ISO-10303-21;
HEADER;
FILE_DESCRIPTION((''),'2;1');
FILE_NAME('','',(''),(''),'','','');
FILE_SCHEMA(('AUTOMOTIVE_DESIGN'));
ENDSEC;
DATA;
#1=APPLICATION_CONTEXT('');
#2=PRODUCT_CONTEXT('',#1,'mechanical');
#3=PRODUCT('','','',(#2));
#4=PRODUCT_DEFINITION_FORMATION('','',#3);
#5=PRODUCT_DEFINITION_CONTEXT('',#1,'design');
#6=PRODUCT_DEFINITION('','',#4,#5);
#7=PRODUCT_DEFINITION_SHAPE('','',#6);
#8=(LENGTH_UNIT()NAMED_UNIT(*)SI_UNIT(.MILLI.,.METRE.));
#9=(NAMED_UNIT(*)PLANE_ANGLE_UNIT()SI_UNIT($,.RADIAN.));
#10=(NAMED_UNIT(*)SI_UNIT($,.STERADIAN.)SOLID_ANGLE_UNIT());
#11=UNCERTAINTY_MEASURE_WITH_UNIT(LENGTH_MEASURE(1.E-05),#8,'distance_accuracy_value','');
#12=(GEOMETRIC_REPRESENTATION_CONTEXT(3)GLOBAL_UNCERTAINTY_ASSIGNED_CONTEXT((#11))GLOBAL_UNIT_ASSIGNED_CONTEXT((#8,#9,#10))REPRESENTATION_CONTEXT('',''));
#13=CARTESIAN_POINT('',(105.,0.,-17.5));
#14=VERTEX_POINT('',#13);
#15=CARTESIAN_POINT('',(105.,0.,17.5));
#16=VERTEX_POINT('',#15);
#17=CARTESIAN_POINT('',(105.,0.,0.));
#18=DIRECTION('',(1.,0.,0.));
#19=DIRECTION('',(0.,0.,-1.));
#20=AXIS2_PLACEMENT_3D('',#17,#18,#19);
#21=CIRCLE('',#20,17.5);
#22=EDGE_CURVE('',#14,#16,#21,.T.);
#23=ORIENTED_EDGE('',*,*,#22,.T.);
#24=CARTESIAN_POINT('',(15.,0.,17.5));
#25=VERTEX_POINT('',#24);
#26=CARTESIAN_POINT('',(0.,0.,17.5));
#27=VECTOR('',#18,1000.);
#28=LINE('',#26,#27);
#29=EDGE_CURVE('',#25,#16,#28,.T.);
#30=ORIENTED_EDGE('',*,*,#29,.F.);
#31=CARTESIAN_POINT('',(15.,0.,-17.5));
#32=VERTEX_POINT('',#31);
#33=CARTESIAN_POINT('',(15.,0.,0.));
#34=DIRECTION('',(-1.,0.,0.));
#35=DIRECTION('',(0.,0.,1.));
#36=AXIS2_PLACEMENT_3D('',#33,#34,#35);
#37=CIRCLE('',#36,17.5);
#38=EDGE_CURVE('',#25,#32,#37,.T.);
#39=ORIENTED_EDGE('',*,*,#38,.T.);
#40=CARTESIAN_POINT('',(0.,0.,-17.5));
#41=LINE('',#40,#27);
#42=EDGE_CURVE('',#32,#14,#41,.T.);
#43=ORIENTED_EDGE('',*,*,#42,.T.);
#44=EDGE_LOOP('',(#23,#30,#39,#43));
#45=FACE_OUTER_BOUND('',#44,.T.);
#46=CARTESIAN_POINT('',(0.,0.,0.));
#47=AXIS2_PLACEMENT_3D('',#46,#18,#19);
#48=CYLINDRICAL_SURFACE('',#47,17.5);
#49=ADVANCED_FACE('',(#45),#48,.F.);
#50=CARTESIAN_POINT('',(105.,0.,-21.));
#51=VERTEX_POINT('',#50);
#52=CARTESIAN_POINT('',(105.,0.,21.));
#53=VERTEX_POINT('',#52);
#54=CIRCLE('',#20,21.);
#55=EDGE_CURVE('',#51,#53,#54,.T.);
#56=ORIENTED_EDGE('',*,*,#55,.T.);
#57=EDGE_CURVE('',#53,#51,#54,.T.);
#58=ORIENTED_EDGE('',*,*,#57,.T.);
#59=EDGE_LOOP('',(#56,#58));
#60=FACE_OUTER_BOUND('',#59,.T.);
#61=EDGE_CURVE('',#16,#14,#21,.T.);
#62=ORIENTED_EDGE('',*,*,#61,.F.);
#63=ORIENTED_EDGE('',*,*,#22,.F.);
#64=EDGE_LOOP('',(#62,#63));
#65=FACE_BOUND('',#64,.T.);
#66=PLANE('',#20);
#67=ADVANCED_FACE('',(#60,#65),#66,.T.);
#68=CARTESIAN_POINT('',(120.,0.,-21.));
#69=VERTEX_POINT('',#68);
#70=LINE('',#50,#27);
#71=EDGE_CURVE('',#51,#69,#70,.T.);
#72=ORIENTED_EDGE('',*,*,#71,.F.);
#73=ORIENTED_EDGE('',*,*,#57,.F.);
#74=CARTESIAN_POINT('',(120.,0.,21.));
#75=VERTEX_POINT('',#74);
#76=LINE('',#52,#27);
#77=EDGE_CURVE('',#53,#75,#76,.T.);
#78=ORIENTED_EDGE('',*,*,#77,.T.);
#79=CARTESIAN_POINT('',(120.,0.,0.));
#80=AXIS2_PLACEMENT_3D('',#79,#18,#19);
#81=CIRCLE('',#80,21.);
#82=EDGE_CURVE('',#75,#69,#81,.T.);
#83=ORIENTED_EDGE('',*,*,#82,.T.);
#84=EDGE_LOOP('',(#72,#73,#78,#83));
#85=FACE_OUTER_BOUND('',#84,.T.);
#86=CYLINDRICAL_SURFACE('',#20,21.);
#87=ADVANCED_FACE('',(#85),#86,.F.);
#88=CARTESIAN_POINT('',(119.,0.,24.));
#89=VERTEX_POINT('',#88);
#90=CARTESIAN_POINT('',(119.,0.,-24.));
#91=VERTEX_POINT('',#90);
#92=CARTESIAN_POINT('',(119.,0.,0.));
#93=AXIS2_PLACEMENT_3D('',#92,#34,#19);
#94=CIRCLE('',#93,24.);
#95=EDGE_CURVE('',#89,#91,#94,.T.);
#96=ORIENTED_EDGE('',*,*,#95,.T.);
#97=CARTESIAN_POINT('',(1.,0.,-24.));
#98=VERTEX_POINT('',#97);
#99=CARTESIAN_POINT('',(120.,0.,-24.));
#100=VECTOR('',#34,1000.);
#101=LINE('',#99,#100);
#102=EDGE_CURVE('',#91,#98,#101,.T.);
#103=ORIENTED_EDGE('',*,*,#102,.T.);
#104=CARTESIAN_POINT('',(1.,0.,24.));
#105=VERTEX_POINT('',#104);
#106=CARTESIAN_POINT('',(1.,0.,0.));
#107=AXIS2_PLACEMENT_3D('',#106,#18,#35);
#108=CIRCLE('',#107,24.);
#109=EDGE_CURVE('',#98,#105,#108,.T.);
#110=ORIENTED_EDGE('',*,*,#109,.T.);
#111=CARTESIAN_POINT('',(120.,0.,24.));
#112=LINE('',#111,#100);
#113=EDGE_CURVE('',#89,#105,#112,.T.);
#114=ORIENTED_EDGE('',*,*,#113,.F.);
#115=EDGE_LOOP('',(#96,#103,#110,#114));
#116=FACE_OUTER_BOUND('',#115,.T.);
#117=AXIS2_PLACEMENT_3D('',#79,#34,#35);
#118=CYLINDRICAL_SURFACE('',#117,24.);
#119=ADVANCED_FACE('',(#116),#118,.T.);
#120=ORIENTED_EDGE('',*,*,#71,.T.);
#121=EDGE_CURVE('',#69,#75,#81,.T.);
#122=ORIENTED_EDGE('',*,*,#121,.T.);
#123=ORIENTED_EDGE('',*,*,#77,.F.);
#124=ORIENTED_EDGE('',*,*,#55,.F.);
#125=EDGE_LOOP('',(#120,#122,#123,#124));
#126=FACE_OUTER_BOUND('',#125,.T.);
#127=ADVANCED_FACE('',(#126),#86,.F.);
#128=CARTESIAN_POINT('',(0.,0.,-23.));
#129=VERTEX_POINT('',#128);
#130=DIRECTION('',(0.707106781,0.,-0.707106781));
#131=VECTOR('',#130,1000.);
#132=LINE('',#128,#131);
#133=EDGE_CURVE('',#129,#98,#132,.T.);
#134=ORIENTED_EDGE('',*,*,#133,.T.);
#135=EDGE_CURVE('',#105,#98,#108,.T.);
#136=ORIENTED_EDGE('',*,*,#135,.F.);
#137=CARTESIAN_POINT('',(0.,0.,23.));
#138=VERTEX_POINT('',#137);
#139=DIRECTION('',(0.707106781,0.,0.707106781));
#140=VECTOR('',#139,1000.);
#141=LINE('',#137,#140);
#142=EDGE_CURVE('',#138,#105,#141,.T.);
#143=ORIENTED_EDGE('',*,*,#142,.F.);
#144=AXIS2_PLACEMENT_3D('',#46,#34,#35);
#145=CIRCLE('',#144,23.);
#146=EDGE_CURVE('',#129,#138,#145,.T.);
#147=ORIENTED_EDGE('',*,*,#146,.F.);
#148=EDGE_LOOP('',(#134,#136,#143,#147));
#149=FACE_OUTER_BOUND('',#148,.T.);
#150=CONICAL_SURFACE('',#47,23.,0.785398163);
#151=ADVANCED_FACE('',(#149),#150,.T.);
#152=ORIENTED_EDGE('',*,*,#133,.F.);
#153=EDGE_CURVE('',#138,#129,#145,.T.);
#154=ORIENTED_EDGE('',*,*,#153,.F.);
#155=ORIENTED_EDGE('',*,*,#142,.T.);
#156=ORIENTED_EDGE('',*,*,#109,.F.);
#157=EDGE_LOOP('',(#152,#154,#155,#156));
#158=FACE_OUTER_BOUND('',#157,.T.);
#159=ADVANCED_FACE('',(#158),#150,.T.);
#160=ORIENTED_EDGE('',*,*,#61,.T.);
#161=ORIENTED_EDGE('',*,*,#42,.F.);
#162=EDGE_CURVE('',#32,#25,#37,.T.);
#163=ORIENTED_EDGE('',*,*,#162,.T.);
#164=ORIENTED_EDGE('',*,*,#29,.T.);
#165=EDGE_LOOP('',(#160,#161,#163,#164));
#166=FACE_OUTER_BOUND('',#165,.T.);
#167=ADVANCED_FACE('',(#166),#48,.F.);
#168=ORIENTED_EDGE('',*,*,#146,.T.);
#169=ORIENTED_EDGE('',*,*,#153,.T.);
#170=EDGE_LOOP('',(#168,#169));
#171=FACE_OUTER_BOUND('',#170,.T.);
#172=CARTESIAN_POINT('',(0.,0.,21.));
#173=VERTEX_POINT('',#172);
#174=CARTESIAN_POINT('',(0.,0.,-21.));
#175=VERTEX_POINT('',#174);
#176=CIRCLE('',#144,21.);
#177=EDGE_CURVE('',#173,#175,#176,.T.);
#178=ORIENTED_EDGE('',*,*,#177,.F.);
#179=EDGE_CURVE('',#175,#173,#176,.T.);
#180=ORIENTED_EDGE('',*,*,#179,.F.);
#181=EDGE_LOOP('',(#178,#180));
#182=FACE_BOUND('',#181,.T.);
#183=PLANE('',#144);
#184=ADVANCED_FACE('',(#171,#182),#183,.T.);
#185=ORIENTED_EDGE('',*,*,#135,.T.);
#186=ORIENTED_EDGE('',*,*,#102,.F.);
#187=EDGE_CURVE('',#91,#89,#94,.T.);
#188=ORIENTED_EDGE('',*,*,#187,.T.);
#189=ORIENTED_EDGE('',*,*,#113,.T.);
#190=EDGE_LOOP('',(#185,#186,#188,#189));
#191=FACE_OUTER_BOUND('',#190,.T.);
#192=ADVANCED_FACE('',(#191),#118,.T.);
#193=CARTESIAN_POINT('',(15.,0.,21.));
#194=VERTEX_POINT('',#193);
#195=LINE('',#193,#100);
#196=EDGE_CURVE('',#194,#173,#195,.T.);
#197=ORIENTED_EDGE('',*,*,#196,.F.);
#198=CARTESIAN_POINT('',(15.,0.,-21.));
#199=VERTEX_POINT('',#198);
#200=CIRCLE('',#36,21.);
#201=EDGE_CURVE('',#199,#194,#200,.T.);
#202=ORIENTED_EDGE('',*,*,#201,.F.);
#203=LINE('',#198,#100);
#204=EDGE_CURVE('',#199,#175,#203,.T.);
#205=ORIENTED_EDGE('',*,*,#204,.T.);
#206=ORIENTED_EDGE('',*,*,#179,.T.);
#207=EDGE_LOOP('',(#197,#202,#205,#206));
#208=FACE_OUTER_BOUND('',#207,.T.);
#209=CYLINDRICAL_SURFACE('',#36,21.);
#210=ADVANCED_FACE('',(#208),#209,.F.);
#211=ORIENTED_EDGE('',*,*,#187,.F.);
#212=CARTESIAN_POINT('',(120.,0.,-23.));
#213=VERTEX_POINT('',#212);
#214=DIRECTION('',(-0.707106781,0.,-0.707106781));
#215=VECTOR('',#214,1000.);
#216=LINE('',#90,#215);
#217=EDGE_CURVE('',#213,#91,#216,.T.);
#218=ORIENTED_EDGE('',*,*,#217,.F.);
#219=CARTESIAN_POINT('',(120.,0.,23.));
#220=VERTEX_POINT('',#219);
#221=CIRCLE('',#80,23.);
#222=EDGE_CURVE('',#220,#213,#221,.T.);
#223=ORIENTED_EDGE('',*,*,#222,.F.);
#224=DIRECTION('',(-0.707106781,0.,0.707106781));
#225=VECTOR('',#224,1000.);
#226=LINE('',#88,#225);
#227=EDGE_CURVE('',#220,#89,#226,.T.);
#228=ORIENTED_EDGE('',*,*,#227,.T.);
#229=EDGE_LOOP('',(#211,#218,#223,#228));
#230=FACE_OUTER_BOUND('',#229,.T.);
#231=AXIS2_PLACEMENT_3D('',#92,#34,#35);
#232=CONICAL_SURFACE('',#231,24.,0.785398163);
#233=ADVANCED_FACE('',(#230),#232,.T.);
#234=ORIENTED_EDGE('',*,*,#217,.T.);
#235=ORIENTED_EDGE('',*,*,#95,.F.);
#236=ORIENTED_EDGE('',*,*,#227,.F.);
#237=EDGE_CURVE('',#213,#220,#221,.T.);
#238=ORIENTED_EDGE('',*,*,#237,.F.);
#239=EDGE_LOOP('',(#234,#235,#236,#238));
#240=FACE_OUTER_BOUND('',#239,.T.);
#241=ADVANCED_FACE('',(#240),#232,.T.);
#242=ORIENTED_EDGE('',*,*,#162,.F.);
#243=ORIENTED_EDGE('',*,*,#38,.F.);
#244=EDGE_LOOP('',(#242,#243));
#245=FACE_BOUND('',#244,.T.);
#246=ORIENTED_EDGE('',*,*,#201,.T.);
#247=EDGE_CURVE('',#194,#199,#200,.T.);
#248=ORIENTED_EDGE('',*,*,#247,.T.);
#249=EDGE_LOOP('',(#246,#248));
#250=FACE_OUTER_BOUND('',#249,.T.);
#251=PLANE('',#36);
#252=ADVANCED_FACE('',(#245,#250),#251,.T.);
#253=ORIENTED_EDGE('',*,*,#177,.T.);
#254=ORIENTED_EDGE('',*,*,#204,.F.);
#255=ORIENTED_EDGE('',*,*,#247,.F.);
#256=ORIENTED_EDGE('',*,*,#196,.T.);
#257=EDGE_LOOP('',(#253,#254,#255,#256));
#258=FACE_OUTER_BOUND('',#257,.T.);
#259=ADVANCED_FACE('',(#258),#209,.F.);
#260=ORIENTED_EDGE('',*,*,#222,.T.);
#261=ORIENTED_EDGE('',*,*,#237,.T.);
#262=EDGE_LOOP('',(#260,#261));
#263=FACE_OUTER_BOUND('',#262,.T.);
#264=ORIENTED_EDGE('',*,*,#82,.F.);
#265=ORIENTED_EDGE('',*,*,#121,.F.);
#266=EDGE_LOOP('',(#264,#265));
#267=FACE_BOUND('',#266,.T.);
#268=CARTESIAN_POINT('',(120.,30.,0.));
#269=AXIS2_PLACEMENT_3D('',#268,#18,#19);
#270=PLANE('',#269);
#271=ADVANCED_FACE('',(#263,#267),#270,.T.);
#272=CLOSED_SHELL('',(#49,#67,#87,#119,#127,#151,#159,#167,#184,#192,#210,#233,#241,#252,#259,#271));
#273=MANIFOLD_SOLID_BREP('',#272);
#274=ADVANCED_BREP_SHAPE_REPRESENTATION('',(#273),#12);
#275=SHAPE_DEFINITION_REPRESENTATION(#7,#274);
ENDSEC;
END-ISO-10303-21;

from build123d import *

# Parameters (mm, degrees)
SKETCH1_W          = 120
SKETCH1_H          = 30
SKETCH2_R          = 21
CUT_EXTRUDE1_DEPTH = 15
CUT_EXTRUDE2_START = -15
SKETCH4_R          = 21
CUT_EXTRUDE2_DEPTH = 15
SKETCH5_R          = 17.5
CUT_EXTRUDE3_DEPTH = 114.247516529
SKETCH8_R          = 41.443957881
SKETCH8_R_2        = 24
CUT_EXTRUDE4_DEPTH = 128.279220614
CHAMFER1_SIZE      = 1
CHAMFER3_SIZE      = 1


with BuildPart() as part:
    # Sketch1 → Revolve1 (revolve)
    with BuildSketch(Plane.XY, mode=Mode.PRIVATE) as revolve1_sk:
        with Locations((60, 15)):
            Rectangle(SKETCH1_W, SKETCH1_H)
    revolve(revolve1_sk.sketch.rotate(Axis((0, 0, 0), (-1, 0, 0)), 90), axis=Axis((0, 0, 0), (-1, 0, 0)))

    # Sketch2 → Cut-Extrude1 (cut)
    with BuildSketch(Plane.ZY):
        Circle(SKETCH2_R)
    extrude(amount=-CUT_EXTRUDE1_DEPTH, mode=Mode.SUBTRACT)

    # Sketch4 → Cut-Extrude2 (cut)
    with BuildSketch(Plane(origin=(120, 0, 0), x_dir=(0, 0, -1), z_dir=(1, 0, 0)).offset(CUT_EXTRUDE2_START)):
        with Locations(Location((0, 0, 0), (0, 0, 180))):
            Circle(SKETCH4_R)
    extrude(amount=CUT_EXTRUDE2_DEPTH, mode=Mode.SUBTRACT)

    # Sketch5 → Cut-Extrude3 (cut, through all)
    with BuildSketch(Plane(origin=(105, 0, 0), x_dir=(0, 0, -1), z_dir=(1, 0, 0))):
        Circle(SKETCH5_R)
    extrude(amount=-CUT_EXTRUDE3_DEPTH, mode=Mode.SUBTRACT)

    # Sketch8 → Cut-Extrude4 (cut, through all)
    with BuildSketch(Plane.ZY):
        Circle(SKETCH8_R)
        Circle(SKETCH8_R_2, mode=Mode.SUBTRACT)
    extrude(amount=-CUT_EXTRUDE4_DEPTH, mode=Mode.SUBTRACT)

    # Chamfer1
    chamfer1_edges = [part.edges().sort_by_distance(p)[0] for p in [
        (0, 0, -24),
    ]]
    chamfer(chamfer1_edges, length=CHAMFER1_SIZE)

    # Chamfer3
    chamfer3_edges = [part.edges().sort_by_distance(p)[0] for p in [
        (120, 0, -24),
    ]]
    chamfer(chamfer3_edges, length=CHAMFER3_SIZE)


solid = part.part
